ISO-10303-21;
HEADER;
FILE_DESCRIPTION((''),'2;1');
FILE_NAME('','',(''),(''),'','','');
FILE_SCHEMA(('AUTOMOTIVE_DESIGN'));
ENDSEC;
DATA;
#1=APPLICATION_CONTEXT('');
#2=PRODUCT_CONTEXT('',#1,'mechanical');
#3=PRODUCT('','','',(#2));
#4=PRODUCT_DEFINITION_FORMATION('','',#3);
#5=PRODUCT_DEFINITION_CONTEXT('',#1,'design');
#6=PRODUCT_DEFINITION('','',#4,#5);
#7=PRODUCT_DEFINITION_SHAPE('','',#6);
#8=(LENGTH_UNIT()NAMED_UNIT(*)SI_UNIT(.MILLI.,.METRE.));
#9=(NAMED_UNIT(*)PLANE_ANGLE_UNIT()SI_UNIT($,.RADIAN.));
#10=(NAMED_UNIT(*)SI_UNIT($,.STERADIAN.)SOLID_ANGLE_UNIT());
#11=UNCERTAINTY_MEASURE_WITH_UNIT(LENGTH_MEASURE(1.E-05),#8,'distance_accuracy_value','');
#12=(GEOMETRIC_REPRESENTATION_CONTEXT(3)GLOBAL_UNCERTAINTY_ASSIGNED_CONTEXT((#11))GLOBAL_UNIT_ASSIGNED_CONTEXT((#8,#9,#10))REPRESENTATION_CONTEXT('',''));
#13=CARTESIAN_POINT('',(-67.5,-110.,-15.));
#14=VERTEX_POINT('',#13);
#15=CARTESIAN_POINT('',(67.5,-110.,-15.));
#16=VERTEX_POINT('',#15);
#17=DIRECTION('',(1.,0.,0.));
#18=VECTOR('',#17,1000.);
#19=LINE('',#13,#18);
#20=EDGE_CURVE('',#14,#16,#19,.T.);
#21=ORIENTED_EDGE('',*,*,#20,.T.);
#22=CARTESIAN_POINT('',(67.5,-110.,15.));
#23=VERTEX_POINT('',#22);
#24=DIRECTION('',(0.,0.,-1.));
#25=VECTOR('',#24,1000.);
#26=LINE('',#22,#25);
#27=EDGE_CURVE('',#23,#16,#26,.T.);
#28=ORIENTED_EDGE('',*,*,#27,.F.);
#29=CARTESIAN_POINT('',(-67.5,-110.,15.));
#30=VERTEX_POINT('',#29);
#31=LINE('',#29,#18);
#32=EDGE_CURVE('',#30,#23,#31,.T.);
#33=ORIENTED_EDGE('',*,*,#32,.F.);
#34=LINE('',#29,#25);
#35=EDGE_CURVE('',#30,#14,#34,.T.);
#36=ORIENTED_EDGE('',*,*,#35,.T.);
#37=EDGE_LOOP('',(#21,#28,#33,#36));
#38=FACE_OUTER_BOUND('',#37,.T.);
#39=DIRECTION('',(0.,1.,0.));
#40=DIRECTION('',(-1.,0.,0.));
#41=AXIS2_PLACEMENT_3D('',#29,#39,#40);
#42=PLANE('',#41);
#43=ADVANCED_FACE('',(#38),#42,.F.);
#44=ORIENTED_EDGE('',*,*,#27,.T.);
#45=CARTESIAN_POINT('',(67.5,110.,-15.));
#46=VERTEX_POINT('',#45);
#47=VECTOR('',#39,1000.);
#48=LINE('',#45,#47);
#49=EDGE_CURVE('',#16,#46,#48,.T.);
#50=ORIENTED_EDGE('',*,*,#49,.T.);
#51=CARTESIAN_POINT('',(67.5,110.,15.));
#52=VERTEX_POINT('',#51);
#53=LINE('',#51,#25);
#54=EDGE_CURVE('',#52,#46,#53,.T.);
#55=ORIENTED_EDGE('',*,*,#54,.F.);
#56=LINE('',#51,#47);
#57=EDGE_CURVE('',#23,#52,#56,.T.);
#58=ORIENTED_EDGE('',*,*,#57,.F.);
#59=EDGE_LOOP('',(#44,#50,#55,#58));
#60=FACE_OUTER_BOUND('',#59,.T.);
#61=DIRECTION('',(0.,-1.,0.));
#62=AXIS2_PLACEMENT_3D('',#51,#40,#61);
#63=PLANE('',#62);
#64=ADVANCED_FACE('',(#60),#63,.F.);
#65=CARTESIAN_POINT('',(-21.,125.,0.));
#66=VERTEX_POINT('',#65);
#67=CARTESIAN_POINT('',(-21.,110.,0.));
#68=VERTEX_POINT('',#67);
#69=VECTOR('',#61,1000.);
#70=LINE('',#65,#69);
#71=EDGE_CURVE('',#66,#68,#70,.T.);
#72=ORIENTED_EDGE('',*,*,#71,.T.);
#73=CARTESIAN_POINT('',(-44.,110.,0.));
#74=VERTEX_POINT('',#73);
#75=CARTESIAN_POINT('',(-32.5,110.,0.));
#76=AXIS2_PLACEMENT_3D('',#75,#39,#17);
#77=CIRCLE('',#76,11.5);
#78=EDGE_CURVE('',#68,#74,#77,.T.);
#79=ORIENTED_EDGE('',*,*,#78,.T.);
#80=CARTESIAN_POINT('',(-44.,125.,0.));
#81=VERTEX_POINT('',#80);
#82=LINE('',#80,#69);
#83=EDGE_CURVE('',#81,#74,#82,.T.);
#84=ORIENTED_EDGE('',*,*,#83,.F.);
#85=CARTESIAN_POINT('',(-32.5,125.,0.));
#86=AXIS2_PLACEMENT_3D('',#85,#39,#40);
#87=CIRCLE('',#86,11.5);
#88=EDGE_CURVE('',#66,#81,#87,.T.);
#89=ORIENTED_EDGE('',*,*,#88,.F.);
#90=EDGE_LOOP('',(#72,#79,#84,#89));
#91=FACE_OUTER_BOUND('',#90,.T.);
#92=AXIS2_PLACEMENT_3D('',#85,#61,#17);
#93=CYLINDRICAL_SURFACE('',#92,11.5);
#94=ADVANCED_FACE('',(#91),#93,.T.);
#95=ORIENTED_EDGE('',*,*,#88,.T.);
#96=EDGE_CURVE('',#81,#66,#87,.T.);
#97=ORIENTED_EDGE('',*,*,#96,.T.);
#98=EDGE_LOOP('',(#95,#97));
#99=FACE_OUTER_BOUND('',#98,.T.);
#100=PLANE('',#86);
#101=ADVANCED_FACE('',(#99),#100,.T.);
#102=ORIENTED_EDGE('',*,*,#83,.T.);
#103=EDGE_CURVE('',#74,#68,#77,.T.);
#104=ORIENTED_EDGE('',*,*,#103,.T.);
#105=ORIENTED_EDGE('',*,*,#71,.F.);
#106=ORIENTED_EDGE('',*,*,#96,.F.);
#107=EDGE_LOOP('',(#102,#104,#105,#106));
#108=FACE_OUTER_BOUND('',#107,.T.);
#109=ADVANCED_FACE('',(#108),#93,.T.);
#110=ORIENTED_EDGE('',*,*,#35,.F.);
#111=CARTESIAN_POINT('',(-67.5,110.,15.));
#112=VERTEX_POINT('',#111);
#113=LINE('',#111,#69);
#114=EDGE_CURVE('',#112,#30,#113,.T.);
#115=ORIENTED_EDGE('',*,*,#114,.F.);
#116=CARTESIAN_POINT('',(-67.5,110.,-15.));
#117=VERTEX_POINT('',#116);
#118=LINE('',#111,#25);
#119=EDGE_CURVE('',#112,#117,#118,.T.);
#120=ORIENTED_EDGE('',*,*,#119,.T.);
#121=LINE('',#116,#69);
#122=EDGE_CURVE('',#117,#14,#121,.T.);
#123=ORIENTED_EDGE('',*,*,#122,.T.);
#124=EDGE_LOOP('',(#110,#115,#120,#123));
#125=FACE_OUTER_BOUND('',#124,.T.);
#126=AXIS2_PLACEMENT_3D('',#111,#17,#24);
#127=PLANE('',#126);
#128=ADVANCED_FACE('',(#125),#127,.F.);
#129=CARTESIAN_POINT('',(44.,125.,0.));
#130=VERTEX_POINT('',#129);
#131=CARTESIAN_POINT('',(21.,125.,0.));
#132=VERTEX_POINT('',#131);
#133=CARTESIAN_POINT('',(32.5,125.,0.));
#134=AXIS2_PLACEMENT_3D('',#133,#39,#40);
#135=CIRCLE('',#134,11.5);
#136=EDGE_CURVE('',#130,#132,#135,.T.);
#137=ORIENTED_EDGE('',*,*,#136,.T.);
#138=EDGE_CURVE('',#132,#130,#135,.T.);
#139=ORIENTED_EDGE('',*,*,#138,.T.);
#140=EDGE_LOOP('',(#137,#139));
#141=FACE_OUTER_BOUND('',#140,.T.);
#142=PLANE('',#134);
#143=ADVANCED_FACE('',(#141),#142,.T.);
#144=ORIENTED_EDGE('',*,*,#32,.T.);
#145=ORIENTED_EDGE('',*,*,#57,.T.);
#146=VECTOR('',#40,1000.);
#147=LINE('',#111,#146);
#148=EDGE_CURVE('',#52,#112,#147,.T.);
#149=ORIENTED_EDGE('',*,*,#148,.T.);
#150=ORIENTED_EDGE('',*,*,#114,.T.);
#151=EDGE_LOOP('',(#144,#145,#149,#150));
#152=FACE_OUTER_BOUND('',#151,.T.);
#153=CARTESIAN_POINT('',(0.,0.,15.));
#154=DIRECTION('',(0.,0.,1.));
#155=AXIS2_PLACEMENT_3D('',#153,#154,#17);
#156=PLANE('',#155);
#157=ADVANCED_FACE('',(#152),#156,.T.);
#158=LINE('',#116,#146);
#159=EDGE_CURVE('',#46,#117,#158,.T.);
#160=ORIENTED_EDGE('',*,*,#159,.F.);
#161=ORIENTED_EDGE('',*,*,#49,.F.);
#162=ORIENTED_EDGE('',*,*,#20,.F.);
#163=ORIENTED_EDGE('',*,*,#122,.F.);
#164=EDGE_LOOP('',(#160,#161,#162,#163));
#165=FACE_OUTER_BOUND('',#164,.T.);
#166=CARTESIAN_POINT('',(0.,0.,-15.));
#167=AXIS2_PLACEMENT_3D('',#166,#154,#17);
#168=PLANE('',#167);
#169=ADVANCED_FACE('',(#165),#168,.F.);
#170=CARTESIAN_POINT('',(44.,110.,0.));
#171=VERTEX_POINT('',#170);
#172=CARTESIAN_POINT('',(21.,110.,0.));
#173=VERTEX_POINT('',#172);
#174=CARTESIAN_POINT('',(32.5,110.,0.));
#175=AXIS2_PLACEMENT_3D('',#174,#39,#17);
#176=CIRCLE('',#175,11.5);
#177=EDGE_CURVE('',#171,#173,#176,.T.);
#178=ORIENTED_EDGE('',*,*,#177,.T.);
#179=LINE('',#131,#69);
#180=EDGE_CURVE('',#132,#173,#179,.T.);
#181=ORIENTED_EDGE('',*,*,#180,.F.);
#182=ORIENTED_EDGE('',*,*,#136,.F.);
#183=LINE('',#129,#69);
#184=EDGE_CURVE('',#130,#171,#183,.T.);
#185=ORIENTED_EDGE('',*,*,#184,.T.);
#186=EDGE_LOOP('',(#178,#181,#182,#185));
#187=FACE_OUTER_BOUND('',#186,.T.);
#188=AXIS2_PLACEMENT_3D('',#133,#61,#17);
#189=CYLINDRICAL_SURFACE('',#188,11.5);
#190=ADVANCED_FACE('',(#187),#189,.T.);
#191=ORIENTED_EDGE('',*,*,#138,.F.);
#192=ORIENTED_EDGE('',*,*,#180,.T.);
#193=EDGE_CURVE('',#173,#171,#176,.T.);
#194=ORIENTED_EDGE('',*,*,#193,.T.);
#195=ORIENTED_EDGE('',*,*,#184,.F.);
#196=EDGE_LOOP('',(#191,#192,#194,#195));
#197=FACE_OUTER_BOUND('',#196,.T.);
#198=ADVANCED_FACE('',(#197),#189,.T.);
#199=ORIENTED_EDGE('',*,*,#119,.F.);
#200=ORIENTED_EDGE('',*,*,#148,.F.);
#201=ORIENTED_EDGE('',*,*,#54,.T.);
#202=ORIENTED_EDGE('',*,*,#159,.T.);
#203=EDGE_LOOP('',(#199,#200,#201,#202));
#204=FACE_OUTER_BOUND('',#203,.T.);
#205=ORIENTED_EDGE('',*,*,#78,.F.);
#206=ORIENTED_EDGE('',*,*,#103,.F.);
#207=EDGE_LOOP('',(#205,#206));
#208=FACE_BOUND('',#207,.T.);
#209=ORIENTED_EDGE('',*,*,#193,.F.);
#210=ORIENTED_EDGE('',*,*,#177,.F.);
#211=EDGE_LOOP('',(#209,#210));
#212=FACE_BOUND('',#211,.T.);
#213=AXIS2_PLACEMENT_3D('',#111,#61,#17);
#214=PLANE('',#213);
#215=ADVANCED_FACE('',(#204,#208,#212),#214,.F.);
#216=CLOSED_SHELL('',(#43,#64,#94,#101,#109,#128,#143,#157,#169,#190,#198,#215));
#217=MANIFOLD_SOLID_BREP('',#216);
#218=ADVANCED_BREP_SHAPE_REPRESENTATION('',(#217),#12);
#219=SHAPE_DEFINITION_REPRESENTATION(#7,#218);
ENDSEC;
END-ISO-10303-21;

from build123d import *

# Parameters (mm, degrees)
SKETCH1_W           = 135
SKETCH1_H           = 220
BOSS_EXTRUDE1_DEPTH = 15
SKETCH2_R           = 11.5
BOSS_EXTRUDE2_DEPTH = 15


with BuildPart() as part:
    # Sketch1 → Boss-Extrude1 (new, symmetric)
    with BuildSketch(Plane.XY):
        Rectangle(SKETCH1_W, SKETCH1_H)
    extrude(amount=BOSS_EXTRUDE1_DEPTH, both=True)

    # Sketch2 → Boss-Extrude2 (add)
    with BuildSketch(Plane(origin=(0, 110, 0), x_dir=(1, 0, 0), z_dir=(0, 1, 0))):
        with Locations((32.5, 0)):
            Circle(SKETCH2_R)
        with Locations((-32.5, 0)):
            Circle(SKETCH2_R)
    extrude(amount=BOSS_EXTRUDE2_DEPTH)


solid = part.part
